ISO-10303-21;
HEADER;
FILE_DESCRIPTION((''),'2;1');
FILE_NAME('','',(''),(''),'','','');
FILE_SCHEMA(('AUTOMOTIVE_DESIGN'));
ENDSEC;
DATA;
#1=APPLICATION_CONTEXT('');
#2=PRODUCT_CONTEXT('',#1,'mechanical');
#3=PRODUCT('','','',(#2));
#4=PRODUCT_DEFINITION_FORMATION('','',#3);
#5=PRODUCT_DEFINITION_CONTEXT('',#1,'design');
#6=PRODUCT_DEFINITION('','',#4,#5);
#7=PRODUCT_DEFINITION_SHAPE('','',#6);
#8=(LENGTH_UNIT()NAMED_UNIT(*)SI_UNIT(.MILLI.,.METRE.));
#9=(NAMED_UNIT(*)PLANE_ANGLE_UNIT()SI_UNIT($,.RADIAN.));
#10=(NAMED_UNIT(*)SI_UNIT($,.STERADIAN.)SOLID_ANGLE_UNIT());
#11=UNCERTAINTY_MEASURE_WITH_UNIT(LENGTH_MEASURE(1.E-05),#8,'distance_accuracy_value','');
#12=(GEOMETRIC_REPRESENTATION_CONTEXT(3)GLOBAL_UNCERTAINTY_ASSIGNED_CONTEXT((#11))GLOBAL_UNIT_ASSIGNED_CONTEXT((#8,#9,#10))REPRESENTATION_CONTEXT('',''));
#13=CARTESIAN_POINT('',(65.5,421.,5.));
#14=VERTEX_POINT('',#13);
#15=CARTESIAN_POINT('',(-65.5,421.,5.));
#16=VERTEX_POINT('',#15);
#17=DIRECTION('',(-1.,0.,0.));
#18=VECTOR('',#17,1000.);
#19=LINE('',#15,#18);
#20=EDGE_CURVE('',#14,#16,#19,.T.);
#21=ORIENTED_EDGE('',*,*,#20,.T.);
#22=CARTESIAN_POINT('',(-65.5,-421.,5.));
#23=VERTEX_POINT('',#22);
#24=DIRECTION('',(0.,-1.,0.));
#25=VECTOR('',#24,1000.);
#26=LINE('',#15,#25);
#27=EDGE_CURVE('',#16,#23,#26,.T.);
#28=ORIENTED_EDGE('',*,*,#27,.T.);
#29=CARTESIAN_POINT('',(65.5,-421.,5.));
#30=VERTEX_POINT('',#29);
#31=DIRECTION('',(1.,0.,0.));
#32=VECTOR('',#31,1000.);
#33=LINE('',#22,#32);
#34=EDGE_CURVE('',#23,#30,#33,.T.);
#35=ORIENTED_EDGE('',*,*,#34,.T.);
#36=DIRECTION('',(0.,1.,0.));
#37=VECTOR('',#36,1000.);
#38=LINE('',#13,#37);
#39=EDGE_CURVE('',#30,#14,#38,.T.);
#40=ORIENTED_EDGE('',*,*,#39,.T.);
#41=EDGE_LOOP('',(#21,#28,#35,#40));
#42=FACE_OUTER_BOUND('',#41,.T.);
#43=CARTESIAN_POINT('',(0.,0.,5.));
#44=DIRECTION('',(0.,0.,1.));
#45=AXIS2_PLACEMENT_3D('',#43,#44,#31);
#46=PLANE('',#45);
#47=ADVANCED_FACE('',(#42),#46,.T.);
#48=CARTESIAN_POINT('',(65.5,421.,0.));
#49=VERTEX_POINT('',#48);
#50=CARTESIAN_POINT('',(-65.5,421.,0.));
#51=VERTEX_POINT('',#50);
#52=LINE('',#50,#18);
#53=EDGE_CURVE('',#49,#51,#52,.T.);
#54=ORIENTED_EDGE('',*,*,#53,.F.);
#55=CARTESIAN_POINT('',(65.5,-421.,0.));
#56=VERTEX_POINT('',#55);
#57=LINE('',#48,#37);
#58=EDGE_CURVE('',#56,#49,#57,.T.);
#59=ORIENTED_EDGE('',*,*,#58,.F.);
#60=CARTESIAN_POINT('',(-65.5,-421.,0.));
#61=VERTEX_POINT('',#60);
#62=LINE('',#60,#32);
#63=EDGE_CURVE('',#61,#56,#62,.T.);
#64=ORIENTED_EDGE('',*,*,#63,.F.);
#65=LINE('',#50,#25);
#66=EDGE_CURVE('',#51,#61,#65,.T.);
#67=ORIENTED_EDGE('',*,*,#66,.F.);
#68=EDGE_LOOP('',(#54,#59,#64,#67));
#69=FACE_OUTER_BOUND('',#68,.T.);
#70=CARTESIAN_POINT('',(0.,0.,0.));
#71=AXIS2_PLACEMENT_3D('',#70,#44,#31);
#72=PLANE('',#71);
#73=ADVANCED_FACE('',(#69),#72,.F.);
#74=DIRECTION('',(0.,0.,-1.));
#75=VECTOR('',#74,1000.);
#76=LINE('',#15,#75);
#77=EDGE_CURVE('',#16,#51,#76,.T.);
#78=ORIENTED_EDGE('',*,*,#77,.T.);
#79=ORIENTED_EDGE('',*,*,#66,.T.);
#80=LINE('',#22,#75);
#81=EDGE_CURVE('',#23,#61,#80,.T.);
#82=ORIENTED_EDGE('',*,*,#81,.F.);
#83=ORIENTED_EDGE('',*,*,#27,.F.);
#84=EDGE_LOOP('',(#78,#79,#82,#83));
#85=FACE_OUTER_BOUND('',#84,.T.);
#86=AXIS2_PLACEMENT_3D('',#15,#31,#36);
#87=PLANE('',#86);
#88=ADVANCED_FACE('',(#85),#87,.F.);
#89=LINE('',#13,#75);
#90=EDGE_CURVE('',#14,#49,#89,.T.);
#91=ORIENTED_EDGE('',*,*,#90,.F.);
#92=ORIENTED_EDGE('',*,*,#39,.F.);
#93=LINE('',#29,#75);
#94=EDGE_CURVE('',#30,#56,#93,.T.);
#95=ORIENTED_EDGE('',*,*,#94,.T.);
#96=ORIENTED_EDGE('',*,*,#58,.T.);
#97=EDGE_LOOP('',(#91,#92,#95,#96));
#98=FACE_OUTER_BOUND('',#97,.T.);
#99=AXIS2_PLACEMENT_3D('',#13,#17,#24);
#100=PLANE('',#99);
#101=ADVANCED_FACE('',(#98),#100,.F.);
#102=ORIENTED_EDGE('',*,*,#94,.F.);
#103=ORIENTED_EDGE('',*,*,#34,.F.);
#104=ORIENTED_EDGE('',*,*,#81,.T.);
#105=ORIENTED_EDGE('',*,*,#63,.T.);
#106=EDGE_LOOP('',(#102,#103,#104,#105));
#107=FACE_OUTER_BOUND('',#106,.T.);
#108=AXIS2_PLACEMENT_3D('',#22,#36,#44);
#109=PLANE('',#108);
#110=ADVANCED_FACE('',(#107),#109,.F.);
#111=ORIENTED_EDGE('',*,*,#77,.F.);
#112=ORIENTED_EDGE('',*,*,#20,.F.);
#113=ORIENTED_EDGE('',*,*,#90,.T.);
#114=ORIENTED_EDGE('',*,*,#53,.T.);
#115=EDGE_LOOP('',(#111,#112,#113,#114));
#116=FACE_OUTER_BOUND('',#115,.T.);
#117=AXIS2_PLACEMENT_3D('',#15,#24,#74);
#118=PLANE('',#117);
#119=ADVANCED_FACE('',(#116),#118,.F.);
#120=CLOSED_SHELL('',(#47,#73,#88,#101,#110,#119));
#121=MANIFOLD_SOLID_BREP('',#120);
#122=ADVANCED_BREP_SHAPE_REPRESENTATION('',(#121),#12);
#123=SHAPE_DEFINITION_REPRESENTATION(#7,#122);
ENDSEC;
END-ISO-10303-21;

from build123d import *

# Parameters (mm, degrees)
SKETCH_1_W      = 131
SKETCH_1_H      = 842
EXTRUDE_1_DEPTH = 5


with BuildPart() as part:
    # 草图1 → 凸台-拉伸1 (new body)
    with BuildSketch(Plane.XY):
        Rectangle(SKETCH_1_W, SKETCH_1_H)
    extrude(amount=EXTRUDE_1_DEPTH)


solid = part.part
